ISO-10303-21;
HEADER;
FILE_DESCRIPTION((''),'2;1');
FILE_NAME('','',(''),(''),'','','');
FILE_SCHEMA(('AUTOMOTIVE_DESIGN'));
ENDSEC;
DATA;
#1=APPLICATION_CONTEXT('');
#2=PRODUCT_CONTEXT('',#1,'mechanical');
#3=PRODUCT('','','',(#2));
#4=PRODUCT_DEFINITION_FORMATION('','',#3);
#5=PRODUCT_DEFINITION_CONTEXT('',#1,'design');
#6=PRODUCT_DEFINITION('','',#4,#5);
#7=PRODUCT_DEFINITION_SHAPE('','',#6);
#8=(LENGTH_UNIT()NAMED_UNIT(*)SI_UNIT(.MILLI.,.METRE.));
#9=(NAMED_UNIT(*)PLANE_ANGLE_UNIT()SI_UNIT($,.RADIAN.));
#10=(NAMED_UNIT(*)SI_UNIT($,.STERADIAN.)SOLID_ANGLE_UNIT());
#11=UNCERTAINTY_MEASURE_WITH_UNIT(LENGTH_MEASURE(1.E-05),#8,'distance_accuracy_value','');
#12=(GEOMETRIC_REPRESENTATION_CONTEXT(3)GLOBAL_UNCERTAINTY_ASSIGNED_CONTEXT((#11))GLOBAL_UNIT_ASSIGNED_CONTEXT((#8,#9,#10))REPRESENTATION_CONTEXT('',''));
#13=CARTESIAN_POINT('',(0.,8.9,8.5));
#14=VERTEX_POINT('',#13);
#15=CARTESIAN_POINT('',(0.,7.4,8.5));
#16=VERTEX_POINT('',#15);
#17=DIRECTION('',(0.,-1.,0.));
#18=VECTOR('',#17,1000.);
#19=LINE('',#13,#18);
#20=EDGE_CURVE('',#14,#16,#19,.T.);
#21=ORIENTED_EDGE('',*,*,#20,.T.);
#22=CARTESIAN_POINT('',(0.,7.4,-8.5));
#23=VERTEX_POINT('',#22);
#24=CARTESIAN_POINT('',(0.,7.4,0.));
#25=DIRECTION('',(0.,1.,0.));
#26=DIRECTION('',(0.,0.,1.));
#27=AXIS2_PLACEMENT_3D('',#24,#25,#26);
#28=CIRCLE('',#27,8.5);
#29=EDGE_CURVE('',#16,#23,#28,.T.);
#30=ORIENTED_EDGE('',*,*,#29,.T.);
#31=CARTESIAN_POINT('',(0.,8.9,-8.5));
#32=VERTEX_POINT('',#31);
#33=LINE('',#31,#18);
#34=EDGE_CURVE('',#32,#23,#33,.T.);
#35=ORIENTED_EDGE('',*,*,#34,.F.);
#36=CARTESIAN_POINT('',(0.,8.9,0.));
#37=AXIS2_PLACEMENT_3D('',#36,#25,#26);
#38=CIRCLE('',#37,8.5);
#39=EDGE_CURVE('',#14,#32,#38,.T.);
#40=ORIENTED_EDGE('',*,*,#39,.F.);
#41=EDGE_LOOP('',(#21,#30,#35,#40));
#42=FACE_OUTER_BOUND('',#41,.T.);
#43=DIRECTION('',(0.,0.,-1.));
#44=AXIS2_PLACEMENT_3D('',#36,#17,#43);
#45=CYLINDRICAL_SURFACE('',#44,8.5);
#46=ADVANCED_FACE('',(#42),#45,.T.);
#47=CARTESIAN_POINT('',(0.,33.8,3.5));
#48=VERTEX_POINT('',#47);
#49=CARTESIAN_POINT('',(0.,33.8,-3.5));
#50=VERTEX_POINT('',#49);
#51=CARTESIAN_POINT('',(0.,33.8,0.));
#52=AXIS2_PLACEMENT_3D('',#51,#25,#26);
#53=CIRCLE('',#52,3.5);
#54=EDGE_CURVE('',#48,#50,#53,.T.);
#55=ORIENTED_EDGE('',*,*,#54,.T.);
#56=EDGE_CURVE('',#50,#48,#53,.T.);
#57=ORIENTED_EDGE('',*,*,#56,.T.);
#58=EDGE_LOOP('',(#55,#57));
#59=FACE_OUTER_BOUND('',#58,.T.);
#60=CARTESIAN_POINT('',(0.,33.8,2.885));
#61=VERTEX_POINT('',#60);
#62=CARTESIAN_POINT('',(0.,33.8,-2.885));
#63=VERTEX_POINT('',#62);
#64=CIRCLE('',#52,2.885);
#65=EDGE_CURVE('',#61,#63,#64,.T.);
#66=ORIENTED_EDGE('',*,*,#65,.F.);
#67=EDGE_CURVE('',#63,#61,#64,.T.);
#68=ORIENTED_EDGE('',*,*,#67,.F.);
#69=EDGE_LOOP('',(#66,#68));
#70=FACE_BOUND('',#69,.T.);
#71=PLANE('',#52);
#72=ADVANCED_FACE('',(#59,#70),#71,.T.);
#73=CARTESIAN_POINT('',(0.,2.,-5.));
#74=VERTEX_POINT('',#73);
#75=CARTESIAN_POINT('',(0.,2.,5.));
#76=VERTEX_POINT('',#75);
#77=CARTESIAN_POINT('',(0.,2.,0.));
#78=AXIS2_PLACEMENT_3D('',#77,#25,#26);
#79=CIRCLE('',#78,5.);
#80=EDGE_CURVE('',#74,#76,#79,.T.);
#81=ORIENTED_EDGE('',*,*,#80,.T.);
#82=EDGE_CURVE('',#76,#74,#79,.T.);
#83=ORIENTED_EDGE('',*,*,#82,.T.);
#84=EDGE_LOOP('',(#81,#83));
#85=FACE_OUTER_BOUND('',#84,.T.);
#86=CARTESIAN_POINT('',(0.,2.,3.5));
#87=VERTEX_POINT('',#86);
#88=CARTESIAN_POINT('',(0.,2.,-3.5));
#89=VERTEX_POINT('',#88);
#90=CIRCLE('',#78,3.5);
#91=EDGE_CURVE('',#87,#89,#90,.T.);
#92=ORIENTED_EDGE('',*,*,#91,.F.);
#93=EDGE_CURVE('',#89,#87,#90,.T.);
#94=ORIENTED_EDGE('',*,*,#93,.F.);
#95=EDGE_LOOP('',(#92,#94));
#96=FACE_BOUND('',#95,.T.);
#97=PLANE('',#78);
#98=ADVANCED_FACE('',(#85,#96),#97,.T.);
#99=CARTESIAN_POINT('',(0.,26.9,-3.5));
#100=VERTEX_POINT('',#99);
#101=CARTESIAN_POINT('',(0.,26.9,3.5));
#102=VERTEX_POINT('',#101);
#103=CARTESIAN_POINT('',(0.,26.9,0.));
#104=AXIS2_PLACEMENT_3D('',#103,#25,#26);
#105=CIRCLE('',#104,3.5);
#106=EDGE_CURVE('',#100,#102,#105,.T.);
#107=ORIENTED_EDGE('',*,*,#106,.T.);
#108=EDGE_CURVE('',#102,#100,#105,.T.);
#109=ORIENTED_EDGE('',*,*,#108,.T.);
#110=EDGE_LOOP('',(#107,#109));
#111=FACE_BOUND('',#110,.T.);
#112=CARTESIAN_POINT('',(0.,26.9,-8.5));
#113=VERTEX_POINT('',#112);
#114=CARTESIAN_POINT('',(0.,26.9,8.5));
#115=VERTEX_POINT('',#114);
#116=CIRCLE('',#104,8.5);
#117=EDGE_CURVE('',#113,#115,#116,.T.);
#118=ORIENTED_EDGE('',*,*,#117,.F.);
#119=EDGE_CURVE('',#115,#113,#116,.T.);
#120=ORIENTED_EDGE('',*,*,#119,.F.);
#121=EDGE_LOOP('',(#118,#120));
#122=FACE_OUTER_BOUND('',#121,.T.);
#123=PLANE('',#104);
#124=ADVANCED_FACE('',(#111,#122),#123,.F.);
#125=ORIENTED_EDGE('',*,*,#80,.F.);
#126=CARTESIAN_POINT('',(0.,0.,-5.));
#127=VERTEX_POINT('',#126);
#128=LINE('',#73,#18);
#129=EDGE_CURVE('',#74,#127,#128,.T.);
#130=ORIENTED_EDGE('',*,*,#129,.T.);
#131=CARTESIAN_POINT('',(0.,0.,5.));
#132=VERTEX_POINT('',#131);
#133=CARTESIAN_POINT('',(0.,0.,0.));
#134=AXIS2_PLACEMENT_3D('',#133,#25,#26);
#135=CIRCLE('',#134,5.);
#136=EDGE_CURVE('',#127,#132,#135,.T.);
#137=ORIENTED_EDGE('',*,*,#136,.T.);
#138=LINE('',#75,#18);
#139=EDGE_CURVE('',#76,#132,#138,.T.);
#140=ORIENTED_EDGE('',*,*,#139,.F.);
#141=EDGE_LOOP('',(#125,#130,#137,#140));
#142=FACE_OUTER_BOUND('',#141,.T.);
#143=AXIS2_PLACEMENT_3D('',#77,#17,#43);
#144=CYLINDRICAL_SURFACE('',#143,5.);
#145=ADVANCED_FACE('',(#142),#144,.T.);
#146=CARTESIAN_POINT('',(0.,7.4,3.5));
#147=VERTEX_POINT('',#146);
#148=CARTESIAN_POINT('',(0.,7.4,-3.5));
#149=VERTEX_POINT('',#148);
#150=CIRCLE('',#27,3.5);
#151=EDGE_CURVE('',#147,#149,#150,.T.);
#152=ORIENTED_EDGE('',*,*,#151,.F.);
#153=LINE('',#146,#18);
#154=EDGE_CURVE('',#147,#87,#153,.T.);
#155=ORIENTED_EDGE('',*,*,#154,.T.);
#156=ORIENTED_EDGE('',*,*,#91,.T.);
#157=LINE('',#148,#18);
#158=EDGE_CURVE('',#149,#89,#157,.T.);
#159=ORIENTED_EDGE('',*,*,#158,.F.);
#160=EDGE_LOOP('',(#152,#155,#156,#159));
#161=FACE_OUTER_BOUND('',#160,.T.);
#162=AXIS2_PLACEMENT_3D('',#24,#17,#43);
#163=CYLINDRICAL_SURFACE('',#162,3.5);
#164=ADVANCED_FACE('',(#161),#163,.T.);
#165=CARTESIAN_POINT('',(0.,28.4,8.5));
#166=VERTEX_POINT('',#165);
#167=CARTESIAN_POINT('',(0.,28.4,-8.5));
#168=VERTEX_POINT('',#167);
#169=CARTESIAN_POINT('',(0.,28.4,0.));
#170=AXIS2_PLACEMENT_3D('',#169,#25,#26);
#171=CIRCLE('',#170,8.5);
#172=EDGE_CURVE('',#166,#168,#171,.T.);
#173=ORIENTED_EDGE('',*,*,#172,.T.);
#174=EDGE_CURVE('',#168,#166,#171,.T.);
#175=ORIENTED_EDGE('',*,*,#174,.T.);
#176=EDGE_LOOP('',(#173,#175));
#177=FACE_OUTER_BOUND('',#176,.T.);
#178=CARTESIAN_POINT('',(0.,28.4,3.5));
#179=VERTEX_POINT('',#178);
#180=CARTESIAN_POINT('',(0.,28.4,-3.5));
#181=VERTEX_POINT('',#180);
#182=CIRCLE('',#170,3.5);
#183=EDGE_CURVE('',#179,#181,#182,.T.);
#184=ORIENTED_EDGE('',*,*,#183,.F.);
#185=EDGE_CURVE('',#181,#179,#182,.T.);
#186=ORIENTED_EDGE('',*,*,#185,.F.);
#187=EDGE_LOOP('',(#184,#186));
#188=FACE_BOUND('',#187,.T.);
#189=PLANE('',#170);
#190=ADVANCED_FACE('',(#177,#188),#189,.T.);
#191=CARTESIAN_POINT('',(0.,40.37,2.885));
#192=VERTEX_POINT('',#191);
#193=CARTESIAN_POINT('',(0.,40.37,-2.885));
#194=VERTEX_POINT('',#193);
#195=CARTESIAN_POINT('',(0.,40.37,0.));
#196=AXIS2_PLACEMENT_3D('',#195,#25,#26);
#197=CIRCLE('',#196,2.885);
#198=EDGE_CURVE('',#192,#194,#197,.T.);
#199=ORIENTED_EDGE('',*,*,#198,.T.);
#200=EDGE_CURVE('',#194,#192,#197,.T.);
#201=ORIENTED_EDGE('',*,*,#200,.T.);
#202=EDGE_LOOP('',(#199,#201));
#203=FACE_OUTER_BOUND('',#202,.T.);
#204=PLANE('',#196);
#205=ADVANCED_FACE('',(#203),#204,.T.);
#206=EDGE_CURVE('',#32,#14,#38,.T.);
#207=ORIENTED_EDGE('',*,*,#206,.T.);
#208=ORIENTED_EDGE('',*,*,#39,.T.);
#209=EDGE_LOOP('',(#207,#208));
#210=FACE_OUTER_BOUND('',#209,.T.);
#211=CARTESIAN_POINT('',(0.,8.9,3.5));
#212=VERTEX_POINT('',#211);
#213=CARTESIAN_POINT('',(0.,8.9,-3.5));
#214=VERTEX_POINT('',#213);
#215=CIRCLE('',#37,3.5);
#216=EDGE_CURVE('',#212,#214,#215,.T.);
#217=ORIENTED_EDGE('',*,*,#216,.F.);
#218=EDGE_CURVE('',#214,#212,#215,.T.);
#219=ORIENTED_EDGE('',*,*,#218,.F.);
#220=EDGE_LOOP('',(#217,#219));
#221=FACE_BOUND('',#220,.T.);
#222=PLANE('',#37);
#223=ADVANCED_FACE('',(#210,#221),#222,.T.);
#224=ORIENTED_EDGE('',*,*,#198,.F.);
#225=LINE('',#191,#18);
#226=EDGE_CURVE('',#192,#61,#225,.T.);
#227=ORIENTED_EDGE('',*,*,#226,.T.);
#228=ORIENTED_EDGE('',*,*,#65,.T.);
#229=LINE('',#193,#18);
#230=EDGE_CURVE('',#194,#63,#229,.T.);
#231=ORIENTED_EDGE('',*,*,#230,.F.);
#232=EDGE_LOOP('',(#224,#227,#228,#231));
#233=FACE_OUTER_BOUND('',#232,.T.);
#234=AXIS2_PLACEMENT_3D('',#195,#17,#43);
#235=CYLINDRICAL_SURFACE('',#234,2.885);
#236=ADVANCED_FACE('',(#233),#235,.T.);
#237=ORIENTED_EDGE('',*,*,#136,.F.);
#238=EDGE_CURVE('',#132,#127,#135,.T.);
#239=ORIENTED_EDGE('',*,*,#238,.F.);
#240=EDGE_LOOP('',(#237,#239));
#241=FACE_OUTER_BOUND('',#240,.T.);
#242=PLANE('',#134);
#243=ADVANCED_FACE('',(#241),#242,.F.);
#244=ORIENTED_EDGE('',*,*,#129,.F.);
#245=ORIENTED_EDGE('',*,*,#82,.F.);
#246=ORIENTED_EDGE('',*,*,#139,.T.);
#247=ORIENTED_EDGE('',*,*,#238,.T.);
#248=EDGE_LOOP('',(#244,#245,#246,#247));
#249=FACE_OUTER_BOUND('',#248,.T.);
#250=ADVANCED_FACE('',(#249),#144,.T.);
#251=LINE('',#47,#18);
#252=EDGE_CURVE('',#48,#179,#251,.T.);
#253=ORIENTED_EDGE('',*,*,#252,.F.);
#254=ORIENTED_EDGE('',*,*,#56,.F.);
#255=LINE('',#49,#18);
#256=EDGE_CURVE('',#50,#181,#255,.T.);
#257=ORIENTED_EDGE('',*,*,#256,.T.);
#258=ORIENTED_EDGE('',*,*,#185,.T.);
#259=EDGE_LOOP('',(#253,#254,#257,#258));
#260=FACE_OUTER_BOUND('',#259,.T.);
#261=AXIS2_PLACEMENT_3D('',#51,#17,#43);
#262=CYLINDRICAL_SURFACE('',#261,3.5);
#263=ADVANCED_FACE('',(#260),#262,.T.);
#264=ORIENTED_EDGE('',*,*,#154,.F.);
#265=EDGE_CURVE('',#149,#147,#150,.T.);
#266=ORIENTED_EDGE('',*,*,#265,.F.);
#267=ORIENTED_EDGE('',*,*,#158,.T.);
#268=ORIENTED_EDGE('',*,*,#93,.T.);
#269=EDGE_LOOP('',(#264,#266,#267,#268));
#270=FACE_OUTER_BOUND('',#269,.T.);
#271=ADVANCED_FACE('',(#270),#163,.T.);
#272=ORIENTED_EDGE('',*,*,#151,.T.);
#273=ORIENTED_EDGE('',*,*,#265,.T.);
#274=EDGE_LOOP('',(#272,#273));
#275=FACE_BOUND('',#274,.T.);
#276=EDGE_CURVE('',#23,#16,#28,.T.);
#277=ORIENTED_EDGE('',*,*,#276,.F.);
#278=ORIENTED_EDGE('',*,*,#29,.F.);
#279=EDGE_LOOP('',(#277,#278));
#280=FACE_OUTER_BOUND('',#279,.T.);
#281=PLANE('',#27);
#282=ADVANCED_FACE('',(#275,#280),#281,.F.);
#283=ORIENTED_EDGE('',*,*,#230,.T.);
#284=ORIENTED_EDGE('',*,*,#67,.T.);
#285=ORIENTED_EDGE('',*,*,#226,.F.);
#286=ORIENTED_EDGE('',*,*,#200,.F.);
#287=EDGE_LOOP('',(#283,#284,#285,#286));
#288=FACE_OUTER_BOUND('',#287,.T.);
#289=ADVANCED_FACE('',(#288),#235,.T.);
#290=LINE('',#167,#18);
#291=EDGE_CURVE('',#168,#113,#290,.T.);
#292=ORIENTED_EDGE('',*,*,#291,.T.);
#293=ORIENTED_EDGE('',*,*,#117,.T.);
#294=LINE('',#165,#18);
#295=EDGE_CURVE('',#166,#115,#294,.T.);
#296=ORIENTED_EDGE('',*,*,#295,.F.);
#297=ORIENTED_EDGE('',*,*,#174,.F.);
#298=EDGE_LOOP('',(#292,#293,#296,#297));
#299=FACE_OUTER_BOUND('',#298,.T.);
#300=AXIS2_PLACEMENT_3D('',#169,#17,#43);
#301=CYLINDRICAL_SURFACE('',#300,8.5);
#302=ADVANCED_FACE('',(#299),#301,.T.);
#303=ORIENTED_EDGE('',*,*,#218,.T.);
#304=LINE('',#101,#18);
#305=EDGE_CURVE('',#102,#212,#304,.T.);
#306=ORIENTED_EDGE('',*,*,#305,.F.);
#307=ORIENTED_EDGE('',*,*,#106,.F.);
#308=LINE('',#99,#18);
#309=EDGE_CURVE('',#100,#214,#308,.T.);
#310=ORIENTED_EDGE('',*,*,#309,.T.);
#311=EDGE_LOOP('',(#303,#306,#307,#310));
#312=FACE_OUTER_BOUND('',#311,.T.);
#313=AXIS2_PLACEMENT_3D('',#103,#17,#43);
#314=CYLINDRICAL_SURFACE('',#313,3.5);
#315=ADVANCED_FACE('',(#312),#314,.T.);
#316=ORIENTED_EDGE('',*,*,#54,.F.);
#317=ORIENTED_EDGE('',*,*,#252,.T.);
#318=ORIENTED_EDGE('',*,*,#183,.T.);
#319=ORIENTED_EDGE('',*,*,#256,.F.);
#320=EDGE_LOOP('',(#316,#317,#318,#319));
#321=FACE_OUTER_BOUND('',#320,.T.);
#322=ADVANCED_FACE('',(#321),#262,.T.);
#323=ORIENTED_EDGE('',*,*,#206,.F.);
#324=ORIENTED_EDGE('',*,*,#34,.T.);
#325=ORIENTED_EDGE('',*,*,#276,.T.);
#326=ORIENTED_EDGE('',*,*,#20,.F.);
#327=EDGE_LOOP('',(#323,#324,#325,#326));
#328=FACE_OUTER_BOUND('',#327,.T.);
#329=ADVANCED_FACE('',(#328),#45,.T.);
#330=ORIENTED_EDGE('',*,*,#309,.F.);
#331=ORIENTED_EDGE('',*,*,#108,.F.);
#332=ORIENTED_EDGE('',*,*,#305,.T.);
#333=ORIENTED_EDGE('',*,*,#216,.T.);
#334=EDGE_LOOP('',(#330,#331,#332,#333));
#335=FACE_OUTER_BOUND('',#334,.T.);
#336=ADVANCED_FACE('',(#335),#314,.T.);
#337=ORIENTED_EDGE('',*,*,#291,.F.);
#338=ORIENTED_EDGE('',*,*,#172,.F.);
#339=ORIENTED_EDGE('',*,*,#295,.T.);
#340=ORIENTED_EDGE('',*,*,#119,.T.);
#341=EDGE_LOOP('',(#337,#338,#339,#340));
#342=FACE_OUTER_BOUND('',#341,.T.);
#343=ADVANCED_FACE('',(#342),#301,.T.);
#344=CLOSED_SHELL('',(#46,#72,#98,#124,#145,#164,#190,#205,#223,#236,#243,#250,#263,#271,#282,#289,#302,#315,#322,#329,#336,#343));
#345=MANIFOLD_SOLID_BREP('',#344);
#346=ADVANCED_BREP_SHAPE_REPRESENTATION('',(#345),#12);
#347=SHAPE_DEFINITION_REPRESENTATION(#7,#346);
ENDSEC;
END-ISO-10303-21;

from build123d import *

# Parameters (mm, degrees)
SKETCH1_R           = 5
BOSS_EXTRUDE1_DEPTH = 2
SKETCH2_R           = 3.5
BOSS_EXTRUDE2_DEPTH = 5.4
SKETCH3_R           = 8.5
BOSS_EXTRUDE3_DEPTH = 1.5
SKETCH4_R           = 3.5
BOSS_EXTRUDE4_DEPTH = 18
SKETCH5_R           = 8.5
BOSS_EXTRUDE5_DEPTH = 1.5
SKETCH6_R           = 3.5
BOSS_EXTRUDE6_DEPTH = 5.4
SKETCH7_R           = 2.885
BOSS_EXTRUDE7_DEPTH = 6.57


with BuildPart() as part:
    # Sketch1 → Boss-Extrude1 (new body)
    with BuildSketch(Plane(origin=(0, 0, 0), x_dir=(1, 0, 0), z_dir=(0, 1, 0))):
        with Locations(Location((0, 0, 0), (0, 0, 270))):
            Circle(SKETCH1_R)
    extrude(amount=BOSS_EXTRUDE1_DEPTH)

    # Sketch2 → Boss-Extrude2 (add)
    with BuildSketch(Plane(origin=(0, 2, 0), x_dir=(1, 0, 0), z_dir=(0, 1, 0))):
        with Locations(Location((0, 0, 0), (0, 0, 90))):
            Circle(SKETCH2_R)
    extrude(amount=BOSS_EXTRUDE2_DEPTH)

    # Sketch3 → Boss-Extrude3 (add)
    with BuildSketch(Plane(origin=(0, 7.4, 0), x_dir=(1, 0, 0), z_dir=(0, 1, 0))):
        with Locations(Location((0, 0, 0), (0, 0, 270))):
            Circle(SKETCH3_R)
    extrude(amount=BOSS_EXTRUDE3_DEPTH)

    # Sketch4 → Boss-Extrude4 (add)
    with BuildSketch(Plane(origin=(0, 8.9, 0), x_dir=(1, 0, 0), z_dir=(0, 1, 0))):
        with Locations(Location((0, 0, 0), (0, 0, 90))):
            Circle(SKETCH4_R)
    extrude(amount=BOSS_EXTRUDE4_DEPTH)

    # Sketch5 → Boss-Extrude5 (add)
    with BuildSketch(Plane(origin=(0, 26.9, 0), x_dir=(1, 0, 0), z_dir=(0, 1, 0))):
        with Locations(Location((0, 0, 0), (0, 0, 270))):
            Circle(SKETCH5_R)
    extrude(amount=BOSS_EXTRUDE5_DEPTH)

    # Sketch6 → Boss-Extrude6 (add)
    with BuildSketch(Plane(origin=(0, 28.4, 0), x_dir=(1, 0, 0), z_dir=(0, 1, 0))):
        with Locations(Location((0, 0, 0), (0, 0, 90))):
            Circle(SKETCH6_R)
    extrude(amount=BOSS_EXTRUDE6_DEPTH)

    # Sketch7 → Boss-Extrude7 (add)
    with BuildSketch(Plane(origin=(0, 33.8, 0), x_dir=(1, 0, 0), z_dir=(0, 1, 0))):
        with Locations(Location((0, 0, 0), (0, 0, 270))):
            Circle(SKETCH7_R)
    extrude(amount=BOSS_EXTRUDE7_DEPTH)


solid = part.part
